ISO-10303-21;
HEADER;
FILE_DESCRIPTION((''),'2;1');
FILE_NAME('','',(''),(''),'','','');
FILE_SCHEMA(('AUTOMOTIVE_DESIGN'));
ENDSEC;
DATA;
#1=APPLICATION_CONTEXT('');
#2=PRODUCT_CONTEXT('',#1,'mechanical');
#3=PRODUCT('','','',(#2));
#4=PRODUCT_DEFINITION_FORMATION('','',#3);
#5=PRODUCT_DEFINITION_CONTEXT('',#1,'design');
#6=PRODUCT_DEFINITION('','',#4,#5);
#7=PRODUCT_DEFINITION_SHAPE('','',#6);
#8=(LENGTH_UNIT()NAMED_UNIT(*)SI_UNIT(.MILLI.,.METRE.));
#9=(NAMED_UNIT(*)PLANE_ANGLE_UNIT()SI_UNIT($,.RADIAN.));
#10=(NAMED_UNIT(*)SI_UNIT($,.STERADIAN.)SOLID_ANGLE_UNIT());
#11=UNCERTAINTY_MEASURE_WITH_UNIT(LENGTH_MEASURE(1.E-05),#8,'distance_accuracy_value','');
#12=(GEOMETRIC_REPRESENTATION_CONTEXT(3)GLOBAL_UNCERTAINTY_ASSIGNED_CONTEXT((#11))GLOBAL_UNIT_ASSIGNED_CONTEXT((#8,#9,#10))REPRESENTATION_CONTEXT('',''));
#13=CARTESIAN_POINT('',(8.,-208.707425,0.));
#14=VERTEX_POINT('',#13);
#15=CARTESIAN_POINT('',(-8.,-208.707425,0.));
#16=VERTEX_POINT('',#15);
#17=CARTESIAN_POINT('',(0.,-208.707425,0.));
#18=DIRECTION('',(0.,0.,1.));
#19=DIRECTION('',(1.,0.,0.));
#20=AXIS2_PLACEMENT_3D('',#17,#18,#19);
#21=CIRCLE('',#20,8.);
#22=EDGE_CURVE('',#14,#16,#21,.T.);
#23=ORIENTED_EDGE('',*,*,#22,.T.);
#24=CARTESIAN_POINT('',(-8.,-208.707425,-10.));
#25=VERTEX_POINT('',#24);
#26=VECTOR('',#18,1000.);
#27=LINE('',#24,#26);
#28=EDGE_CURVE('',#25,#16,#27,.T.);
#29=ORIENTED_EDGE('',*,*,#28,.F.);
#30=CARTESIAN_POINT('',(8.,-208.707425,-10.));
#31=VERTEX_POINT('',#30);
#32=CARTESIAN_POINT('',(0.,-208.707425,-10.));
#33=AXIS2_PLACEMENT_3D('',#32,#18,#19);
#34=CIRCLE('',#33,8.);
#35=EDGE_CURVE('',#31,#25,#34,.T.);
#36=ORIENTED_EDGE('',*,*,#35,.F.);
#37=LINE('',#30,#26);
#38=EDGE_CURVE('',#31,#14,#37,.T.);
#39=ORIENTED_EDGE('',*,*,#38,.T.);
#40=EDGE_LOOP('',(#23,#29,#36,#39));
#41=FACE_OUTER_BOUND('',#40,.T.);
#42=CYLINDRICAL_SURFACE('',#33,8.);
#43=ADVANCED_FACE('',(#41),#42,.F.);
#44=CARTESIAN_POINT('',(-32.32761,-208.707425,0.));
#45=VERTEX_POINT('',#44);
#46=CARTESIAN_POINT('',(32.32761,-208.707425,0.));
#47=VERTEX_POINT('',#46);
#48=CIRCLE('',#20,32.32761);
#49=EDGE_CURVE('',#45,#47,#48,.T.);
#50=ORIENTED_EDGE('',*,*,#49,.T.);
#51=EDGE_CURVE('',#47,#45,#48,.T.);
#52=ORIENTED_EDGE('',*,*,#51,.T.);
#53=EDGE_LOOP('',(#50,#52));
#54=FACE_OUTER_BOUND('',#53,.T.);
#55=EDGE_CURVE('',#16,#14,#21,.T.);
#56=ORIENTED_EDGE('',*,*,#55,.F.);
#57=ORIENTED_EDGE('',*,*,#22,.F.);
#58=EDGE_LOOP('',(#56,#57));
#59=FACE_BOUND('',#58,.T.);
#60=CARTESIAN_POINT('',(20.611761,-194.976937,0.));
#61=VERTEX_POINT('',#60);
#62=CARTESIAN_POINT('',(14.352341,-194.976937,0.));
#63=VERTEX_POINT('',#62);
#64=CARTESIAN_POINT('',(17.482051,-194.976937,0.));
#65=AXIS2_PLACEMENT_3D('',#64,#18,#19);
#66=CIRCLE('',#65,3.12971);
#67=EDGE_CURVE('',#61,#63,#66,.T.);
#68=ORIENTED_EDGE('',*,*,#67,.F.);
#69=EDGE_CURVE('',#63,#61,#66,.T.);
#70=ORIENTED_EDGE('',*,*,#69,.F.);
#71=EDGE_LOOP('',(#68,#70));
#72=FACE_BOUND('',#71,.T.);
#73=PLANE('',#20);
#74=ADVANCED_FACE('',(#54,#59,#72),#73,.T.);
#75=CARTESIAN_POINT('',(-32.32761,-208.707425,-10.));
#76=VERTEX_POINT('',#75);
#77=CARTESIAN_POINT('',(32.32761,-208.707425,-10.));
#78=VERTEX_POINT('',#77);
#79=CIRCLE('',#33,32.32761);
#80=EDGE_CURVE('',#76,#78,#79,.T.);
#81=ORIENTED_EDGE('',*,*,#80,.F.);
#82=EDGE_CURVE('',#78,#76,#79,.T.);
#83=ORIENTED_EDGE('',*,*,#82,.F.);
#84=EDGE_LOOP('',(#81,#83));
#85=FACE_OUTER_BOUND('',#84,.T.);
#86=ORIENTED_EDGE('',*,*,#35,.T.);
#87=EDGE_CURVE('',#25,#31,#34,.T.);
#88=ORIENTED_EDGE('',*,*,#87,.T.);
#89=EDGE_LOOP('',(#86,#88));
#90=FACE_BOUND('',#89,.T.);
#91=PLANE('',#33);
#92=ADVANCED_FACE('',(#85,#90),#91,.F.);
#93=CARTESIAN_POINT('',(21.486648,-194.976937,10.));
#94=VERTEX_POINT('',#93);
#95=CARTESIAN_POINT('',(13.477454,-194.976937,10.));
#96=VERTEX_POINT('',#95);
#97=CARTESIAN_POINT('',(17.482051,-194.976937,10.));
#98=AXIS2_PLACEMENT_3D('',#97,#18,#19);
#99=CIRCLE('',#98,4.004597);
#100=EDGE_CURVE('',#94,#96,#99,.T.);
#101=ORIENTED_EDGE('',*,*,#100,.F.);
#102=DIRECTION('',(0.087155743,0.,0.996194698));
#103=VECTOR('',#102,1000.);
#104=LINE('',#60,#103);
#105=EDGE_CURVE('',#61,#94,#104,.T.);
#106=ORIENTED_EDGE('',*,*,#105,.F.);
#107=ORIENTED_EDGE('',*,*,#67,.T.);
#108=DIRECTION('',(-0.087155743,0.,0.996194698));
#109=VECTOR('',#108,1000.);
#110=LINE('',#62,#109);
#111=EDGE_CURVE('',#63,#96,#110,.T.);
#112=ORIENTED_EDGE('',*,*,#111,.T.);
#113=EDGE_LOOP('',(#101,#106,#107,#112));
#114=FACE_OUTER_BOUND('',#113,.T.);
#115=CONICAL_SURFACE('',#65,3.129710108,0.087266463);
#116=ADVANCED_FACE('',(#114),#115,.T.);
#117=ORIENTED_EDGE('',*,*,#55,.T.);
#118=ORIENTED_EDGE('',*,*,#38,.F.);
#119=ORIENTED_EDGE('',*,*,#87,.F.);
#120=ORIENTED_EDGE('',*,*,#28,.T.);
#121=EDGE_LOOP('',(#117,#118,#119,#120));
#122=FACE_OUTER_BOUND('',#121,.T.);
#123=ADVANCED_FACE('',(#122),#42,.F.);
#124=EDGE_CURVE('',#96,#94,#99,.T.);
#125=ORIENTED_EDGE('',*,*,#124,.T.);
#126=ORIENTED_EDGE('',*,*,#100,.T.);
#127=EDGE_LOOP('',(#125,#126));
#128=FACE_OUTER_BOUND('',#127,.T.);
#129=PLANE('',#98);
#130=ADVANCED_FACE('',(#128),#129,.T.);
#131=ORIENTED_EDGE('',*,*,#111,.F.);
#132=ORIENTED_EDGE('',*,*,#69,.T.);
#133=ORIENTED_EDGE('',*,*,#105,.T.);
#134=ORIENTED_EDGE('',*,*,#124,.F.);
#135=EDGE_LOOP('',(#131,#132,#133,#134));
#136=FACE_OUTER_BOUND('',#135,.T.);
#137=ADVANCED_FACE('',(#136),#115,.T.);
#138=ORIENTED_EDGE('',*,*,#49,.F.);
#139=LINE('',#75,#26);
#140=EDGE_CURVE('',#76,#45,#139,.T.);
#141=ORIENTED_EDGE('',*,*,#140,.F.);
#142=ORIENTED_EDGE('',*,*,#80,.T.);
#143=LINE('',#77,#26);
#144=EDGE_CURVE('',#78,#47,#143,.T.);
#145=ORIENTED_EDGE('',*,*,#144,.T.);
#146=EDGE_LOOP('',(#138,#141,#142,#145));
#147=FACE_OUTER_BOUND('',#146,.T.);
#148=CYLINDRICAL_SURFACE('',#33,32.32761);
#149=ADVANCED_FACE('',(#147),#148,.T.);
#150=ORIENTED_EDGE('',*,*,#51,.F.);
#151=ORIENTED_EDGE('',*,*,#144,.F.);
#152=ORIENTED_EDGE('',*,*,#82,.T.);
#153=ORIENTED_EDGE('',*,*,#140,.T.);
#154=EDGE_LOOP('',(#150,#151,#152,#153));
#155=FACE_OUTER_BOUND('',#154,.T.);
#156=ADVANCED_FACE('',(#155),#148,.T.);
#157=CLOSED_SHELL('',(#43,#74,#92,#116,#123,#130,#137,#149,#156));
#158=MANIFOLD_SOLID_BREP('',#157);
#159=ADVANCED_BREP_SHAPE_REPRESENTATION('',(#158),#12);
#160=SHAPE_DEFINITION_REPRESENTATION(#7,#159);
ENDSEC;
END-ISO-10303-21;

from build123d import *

# Parameters (mm, degrees)
SKETCH1_R           = 32.327609768
SKETCH1_R_2         = 8
BOSS_EXTRUDE1_DEPTH = 10
SKETCH2_R           = 3.129710108
BOSS_EXTRUDE2_DEPTH = 10
BOSS_EXTRUDE2_DRAFT = -5


with BuildPart() as part:
    # Sketch1 → Boss-Extrude1 (new body)
    with BuildSketch(Plane.XY):
        with Locations((0, -208.707425476)):
            Circle(SKETCH1_R)
        with Locations((0, -208.707425476)):
            Circle(SKETCH1_R_2, mode=Mode.SUBTRACT)
    extrude(amount=-BOSS_EXTRUDE1_DEPTH)


with BuildPart() as boss_extrude2_tool:
    # Sketch2 → Boss-Extrude2 (with draft: the straight prism first)
    with BuildSketch(Plane.XY):
        with Locations((17.482051152, -194.976936722)):
            Circle(SKETCH2_R)
    extrude(amount=BOSS_EXTRUDE2_DEPTH)
    # Boss-Extrude2: the draft: its side faces are tilted about the plane it starts from
    boss_extrude2_sides = [boss_extrude2_tool.faces().sort_by_distance(p)[0] for p in [
        (14.352341045, -194.976936722, 5),
    ]]
    draft(boss_extrude2_sides, Plane.XY, BOSS_EXTRUDE2_DRAFT)


with BuildPart() as part_1:
    add(part.part)

    # Boss-Extrude2: add boss_extrude2_tool
    add(boss_extrude2_tool.part)


solid = part_1.part
